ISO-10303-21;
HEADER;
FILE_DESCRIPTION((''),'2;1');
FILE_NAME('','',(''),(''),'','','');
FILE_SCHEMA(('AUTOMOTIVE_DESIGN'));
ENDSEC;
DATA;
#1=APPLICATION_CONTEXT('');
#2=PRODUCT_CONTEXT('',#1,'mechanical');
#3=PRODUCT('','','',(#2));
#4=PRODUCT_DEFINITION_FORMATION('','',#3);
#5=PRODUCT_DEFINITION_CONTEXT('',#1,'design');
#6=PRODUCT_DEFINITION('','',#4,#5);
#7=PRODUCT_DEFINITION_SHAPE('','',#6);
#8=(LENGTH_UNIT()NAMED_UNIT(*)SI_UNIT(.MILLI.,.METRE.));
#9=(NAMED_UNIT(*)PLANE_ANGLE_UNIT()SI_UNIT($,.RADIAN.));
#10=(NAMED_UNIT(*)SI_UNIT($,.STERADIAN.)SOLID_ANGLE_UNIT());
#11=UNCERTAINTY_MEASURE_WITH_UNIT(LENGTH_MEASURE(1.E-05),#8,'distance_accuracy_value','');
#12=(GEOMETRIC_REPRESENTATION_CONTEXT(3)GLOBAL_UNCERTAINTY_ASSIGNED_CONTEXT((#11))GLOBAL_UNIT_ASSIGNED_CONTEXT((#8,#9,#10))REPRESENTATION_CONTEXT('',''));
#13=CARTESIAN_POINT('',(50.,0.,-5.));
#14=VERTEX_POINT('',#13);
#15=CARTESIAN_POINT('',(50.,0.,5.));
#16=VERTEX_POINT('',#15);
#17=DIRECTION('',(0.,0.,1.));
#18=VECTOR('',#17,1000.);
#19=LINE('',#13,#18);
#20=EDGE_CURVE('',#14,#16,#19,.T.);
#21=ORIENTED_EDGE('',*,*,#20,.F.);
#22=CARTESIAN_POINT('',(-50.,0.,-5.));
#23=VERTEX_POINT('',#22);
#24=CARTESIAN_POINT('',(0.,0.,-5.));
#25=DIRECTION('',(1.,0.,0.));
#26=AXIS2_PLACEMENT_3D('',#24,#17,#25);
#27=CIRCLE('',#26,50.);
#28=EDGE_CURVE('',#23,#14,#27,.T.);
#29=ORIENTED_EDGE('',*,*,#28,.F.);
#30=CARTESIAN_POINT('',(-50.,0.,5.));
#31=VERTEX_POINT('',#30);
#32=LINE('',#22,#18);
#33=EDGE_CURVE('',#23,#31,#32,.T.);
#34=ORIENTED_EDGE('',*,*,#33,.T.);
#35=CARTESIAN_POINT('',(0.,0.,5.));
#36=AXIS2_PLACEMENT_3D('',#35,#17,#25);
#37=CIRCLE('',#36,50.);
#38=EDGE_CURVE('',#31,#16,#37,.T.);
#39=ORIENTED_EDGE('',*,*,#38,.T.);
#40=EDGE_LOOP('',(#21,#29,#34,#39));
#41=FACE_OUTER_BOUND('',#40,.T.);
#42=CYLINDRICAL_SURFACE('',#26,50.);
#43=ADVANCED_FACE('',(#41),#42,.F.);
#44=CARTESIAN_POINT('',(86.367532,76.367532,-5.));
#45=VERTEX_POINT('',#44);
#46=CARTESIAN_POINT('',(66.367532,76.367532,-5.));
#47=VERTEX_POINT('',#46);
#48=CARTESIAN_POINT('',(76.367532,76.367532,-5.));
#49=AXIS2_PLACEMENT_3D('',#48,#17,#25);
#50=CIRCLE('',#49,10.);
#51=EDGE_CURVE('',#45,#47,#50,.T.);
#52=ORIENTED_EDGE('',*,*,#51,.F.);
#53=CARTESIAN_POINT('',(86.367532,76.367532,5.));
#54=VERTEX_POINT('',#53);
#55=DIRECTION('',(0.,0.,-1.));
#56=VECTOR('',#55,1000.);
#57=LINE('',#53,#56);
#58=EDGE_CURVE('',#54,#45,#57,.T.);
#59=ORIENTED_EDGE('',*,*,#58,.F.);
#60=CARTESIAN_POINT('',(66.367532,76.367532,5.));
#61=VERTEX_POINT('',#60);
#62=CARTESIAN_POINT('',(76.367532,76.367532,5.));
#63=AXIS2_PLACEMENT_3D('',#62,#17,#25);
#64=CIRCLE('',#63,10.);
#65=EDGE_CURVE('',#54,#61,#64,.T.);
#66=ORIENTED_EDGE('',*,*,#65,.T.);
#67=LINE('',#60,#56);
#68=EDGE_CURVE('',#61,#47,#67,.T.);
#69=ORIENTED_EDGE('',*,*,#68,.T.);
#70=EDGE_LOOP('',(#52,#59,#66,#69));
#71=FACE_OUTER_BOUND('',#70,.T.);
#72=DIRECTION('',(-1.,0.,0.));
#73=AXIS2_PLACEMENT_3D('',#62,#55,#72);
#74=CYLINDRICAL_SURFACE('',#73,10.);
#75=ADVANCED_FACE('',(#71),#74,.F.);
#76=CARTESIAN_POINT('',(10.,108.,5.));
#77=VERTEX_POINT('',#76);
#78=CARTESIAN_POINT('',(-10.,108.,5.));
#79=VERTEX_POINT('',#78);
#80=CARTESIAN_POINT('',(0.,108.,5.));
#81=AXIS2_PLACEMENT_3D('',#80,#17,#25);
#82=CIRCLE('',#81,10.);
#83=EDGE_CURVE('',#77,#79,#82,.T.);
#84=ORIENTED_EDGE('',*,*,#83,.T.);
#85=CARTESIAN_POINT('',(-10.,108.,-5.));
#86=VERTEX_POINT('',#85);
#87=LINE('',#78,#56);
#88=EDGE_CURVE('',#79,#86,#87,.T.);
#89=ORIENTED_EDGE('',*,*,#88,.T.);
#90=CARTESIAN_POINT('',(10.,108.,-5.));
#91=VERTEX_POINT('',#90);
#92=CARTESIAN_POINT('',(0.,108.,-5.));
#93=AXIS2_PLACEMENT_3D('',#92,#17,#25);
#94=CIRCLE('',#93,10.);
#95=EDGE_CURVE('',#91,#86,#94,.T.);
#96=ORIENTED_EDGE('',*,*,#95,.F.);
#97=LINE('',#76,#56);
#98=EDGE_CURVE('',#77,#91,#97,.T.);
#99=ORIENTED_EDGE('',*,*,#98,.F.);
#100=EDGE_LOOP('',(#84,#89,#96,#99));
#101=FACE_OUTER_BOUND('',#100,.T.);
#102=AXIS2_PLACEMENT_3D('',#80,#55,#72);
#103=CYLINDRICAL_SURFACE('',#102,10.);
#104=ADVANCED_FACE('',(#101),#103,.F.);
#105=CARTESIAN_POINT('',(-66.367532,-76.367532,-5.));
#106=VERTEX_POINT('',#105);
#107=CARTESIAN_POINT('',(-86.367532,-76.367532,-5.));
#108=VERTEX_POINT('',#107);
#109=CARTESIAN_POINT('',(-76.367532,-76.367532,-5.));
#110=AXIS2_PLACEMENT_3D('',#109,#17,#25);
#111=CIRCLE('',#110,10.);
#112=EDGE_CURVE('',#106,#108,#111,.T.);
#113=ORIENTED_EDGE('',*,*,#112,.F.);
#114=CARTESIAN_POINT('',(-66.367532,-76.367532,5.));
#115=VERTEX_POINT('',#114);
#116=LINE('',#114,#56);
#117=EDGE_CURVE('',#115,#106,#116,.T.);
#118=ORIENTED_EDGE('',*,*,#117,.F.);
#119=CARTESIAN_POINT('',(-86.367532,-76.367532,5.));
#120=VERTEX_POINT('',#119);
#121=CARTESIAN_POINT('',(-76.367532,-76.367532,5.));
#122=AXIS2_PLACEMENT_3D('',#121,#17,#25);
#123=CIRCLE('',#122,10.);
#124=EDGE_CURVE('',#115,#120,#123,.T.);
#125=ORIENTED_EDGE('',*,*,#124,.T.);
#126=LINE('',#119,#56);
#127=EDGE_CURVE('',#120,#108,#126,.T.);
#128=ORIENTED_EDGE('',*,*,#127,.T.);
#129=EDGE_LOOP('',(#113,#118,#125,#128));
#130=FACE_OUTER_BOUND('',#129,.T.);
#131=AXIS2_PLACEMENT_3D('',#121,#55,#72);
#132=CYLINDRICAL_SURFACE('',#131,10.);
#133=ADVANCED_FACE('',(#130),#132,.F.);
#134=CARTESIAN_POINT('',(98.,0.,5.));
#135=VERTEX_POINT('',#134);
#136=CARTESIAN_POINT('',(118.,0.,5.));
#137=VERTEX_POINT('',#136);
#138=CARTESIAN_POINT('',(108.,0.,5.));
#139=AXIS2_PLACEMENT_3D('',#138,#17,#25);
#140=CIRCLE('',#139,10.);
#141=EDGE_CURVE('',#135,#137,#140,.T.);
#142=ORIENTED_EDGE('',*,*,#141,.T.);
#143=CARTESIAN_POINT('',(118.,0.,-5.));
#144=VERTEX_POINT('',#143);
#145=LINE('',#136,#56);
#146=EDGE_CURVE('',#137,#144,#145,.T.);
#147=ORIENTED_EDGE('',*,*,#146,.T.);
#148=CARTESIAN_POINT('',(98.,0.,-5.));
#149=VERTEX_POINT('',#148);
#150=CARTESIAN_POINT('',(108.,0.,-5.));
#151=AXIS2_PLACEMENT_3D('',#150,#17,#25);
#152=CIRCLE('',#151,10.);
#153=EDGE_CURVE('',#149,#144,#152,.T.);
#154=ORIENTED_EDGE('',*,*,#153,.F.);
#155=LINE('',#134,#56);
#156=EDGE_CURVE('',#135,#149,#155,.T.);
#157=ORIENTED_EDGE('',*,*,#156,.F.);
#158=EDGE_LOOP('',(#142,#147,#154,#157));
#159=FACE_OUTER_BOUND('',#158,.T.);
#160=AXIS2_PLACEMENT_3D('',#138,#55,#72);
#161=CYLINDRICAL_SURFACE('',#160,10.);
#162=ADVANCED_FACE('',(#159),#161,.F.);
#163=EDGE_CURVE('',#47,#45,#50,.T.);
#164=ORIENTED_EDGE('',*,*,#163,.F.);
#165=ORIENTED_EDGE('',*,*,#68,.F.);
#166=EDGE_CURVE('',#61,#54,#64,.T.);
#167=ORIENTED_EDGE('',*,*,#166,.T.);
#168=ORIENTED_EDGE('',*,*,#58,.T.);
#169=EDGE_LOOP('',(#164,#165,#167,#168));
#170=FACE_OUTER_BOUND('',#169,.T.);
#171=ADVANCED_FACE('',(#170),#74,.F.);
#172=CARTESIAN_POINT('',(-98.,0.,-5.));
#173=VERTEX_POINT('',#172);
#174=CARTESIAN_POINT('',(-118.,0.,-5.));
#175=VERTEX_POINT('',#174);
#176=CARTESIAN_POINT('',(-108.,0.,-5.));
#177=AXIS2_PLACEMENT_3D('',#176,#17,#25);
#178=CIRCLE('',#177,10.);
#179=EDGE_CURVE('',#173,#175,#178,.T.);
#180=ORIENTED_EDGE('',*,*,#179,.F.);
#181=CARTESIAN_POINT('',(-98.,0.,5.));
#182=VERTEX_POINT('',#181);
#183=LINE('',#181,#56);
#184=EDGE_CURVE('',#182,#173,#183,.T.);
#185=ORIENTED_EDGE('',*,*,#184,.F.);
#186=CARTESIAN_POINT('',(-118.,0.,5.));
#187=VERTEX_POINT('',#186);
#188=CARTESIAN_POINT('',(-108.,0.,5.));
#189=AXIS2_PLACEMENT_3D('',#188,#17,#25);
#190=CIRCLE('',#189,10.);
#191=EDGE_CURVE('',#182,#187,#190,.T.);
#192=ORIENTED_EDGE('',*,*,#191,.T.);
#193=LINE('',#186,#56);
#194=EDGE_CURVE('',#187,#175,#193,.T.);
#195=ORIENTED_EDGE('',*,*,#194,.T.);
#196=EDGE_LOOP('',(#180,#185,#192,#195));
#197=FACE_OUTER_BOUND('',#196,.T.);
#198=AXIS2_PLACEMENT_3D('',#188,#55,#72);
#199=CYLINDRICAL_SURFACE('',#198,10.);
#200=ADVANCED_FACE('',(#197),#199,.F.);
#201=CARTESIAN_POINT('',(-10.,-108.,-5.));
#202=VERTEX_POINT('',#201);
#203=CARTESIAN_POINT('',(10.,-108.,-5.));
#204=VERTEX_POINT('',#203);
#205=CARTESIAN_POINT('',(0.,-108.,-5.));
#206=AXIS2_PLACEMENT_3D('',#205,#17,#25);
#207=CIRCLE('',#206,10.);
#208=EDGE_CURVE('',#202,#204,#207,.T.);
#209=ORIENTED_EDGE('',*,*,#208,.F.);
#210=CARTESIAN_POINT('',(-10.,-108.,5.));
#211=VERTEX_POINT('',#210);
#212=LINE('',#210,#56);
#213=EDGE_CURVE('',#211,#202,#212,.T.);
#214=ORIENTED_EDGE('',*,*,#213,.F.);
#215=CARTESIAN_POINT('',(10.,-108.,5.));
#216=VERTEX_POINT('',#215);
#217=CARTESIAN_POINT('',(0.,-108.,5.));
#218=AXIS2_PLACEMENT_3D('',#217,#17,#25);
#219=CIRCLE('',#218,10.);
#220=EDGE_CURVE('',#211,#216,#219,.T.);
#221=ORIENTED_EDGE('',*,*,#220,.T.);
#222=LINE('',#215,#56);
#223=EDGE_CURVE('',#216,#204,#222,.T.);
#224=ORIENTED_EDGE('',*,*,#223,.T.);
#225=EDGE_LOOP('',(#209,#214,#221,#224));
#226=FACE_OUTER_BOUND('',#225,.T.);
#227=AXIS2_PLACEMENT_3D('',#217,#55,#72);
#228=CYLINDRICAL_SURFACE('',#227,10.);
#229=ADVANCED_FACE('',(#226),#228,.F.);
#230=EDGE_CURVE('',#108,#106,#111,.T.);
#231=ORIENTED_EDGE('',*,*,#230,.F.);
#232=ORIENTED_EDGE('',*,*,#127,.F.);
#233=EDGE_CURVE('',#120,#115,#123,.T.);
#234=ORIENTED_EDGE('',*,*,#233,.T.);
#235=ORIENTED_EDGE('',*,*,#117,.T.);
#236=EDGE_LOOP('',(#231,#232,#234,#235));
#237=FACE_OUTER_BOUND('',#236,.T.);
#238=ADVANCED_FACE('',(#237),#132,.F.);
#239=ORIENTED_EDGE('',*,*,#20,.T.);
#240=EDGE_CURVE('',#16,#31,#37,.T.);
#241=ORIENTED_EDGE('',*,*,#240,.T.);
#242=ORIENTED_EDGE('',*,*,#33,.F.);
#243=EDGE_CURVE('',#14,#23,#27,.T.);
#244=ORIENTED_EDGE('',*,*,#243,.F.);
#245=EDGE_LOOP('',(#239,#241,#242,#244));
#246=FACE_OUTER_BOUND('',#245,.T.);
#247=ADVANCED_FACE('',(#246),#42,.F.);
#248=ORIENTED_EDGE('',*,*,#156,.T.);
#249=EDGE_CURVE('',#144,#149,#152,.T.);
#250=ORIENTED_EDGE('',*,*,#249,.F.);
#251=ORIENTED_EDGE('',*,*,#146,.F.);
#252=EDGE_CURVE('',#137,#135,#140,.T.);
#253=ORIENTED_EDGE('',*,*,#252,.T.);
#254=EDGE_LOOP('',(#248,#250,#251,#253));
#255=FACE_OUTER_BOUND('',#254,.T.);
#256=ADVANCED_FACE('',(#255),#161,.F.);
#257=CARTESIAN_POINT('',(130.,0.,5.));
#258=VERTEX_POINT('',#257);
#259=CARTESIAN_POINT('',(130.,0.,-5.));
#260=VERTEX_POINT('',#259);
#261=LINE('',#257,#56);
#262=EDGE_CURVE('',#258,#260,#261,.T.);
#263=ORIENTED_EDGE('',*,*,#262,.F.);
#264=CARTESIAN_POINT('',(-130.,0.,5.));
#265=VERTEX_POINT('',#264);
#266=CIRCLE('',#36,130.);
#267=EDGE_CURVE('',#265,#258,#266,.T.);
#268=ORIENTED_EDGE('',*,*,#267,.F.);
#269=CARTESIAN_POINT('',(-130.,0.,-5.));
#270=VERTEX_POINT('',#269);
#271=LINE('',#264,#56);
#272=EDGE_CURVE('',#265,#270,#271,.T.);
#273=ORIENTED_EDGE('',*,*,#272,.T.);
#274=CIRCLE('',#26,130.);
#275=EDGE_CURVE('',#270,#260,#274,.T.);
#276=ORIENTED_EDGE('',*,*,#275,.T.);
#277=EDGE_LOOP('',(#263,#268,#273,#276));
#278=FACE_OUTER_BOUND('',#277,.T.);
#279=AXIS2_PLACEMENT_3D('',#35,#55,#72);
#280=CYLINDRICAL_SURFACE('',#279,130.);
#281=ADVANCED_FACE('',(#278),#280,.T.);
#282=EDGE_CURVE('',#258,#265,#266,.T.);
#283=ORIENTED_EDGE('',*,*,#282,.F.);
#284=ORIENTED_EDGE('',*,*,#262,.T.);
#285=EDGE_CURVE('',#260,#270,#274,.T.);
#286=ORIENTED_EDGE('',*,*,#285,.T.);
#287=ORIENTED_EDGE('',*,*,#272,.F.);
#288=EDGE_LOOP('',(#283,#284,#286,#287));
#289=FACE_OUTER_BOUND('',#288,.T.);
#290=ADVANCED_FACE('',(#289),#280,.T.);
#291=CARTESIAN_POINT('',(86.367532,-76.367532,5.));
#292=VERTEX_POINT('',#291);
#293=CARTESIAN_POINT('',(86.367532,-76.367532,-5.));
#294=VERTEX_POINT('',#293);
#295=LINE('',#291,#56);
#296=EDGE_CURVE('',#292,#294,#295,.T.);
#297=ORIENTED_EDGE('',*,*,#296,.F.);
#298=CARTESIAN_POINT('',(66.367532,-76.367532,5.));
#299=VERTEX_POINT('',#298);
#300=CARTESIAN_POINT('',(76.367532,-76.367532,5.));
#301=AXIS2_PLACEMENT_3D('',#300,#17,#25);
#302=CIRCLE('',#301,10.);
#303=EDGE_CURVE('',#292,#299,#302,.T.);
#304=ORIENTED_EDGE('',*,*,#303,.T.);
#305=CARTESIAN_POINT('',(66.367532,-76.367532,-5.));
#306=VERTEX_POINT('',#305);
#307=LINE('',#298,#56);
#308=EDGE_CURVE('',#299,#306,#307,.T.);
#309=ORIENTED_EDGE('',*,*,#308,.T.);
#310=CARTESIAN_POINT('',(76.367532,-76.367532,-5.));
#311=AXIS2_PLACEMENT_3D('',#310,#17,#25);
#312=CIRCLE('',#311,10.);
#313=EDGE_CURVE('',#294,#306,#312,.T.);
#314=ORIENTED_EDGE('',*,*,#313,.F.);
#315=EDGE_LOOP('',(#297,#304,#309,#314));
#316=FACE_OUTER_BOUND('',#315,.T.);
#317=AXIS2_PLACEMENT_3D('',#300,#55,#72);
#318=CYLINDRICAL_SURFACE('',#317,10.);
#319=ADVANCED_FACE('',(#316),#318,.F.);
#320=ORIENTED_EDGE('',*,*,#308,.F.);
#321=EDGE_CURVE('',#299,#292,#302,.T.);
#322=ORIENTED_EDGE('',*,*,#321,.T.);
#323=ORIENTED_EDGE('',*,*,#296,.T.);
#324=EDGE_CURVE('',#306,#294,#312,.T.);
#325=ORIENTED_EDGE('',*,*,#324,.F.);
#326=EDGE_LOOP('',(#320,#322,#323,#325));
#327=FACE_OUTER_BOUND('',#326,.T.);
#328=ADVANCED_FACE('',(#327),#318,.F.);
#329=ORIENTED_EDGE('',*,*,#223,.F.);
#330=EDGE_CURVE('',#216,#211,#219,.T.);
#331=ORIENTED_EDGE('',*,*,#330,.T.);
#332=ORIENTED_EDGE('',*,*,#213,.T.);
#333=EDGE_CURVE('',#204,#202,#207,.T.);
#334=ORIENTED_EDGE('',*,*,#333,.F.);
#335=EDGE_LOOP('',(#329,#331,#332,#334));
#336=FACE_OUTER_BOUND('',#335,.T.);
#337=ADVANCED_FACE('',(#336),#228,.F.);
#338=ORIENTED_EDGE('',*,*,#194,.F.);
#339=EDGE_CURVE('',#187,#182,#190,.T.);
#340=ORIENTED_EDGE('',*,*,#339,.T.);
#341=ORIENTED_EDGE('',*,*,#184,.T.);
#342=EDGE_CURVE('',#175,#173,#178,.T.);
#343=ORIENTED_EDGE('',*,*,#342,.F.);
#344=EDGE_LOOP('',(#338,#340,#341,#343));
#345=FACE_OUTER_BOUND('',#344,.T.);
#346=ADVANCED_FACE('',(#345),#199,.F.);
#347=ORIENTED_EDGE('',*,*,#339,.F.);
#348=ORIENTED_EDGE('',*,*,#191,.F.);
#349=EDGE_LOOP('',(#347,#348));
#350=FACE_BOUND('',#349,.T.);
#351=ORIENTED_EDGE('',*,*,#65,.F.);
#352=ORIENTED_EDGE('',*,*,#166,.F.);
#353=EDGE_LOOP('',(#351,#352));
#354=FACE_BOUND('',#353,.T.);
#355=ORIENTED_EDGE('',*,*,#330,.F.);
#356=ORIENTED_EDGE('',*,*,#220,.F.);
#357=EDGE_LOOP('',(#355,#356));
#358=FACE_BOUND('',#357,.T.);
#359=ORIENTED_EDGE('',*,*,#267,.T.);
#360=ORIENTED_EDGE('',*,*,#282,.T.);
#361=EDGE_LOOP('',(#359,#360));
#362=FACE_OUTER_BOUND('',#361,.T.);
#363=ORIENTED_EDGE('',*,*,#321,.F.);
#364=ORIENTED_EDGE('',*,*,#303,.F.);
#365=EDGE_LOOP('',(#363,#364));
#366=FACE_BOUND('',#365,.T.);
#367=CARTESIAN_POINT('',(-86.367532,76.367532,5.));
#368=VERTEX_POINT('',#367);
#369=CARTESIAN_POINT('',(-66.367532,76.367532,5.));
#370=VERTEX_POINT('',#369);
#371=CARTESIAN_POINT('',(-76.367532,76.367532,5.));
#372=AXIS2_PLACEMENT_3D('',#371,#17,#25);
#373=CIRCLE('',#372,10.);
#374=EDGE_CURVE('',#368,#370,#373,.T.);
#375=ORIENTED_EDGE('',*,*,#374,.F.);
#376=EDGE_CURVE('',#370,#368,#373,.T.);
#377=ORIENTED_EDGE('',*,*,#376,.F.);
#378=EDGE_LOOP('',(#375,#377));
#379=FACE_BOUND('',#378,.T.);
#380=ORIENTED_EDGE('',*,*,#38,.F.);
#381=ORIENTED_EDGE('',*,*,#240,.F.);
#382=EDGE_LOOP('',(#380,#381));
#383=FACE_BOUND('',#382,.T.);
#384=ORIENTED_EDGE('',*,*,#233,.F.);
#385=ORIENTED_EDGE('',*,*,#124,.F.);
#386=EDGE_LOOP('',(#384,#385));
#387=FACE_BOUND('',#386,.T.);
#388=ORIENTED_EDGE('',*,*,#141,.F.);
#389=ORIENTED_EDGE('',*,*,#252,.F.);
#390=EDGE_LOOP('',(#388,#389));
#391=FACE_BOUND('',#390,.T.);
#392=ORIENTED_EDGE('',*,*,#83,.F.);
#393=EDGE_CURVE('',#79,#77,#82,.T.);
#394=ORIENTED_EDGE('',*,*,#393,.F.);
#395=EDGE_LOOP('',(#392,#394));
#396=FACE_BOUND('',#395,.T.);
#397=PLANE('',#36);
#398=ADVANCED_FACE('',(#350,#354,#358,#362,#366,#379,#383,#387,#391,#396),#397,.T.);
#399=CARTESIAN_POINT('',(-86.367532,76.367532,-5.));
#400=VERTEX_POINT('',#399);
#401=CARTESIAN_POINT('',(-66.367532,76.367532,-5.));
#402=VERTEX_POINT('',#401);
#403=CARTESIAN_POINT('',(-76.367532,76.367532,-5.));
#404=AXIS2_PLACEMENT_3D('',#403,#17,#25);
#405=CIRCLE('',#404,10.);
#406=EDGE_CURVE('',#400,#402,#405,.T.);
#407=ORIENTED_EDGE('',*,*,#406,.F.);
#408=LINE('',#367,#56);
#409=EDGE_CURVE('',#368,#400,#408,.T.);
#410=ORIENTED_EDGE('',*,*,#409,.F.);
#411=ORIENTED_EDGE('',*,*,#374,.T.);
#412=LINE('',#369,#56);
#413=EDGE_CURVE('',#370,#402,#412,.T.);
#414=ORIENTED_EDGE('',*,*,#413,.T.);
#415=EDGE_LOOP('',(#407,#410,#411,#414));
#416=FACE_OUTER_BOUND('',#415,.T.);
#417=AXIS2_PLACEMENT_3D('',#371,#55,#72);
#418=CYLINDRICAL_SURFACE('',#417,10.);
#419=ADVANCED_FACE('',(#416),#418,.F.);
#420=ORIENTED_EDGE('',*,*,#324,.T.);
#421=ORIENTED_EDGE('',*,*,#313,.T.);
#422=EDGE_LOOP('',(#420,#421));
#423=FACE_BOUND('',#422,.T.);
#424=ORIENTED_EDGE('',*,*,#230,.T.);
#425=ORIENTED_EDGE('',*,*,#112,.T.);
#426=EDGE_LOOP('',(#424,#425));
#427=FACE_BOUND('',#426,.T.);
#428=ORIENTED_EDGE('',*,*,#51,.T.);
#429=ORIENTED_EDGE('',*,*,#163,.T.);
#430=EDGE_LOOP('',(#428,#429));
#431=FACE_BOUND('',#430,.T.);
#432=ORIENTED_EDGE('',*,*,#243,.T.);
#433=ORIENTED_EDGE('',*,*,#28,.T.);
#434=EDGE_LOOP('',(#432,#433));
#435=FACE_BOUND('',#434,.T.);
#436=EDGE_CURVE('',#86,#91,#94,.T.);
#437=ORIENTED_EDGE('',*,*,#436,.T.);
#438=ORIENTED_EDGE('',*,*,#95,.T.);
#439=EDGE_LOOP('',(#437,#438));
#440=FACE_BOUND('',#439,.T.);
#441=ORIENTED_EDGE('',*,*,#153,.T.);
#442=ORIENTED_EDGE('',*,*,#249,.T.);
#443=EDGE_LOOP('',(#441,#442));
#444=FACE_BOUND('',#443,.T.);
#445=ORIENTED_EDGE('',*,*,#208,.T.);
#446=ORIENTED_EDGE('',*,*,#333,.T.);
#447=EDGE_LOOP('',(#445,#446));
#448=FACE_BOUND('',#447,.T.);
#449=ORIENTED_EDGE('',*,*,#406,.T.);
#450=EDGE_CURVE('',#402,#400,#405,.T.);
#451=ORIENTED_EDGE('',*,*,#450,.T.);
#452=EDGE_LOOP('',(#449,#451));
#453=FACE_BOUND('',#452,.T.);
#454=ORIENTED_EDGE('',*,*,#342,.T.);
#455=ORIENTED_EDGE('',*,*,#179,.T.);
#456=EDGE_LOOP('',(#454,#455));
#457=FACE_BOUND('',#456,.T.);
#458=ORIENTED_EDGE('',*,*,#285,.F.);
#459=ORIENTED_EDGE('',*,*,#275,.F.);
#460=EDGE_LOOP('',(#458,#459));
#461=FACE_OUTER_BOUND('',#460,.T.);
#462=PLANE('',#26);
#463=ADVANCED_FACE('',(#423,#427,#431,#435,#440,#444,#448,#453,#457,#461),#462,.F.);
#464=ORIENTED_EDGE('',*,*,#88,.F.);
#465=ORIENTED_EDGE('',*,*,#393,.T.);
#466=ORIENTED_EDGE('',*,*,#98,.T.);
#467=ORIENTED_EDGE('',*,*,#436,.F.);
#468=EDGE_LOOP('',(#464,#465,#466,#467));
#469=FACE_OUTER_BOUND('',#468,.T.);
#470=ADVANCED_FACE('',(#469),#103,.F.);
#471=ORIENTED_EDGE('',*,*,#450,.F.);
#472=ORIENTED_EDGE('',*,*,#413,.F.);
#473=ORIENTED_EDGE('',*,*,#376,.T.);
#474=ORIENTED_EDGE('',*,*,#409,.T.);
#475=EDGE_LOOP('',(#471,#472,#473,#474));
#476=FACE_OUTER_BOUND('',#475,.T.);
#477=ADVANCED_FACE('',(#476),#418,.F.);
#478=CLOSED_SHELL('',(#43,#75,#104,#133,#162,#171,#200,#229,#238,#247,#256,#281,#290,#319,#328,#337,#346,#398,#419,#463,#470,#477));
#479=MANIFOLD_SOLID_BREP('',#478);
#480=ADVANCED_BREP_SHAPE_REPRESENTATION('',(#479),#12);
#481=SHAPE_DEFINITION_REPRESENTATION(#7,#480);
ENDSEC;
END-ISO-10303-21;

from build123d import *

# Parameters (mm, degrees)
SKETCH_1_R          = 130
SKETCH_1_R_2        = 10
EXTRUDE_1_DEPTH     = 5
SKETCH_2_R          = 50
CUT_EXTRUDE_1_DEPTH = 10


with BuildPart() as part:
    # 草图1 → 凸台-拉伸1 (new, symmetric)
    with BuildSketch(Plane.XY):
        Circle(SKETCH_1_R)
        with Locations((0, 108)):
            Circle(SKETCH_1_R_2, mode=Mode.SUBTRACT)
        with Locations((76.367532368, 76.367532368)):
            Circle(SKETCH_1_R_2, mode=Mode.SUBTRACT)
        with Locations((108, 0)):
            Circle(SKETCH_1_R_2, mode=Mode.SUBTRACT)
        with Locations((76.367532368, -76.367532368)):
            Circle(SKETCH_1_R_2, mode=Mode.SUBTRACT)
        with Locations((0, -108)):
            Circle(SKETCH_1_R_2, mode=Mode.SUBTRACT)
        with Locations((-76.367532368, -76.367532368)):
            Circle(SKETCH_1_R_2, mode=Mode.SUBTRACT)
        with Locations((-108, 0)):
            Circle(SKETCH_1_R_2, mode=Mode.SUBTRACT)
        with Locations((-76.367532368, 76.367532368)):
            Circle(SKETCH_1_R_2, mode=Mode.SUBTRACT)
    extrude(amount=EXTRUDE_1_DEPTH, both=True)

    # 草图2 → 切除-拉伸1 (cut)
    with BuildSketch(Plane.XY.offset(5)):
        Circle(SKETCH_2_R)
    extrude(amount=-CUT_EXTRUDE_1_DEPTH, mode=Mode.SUBTRACT)


solid = part.part
